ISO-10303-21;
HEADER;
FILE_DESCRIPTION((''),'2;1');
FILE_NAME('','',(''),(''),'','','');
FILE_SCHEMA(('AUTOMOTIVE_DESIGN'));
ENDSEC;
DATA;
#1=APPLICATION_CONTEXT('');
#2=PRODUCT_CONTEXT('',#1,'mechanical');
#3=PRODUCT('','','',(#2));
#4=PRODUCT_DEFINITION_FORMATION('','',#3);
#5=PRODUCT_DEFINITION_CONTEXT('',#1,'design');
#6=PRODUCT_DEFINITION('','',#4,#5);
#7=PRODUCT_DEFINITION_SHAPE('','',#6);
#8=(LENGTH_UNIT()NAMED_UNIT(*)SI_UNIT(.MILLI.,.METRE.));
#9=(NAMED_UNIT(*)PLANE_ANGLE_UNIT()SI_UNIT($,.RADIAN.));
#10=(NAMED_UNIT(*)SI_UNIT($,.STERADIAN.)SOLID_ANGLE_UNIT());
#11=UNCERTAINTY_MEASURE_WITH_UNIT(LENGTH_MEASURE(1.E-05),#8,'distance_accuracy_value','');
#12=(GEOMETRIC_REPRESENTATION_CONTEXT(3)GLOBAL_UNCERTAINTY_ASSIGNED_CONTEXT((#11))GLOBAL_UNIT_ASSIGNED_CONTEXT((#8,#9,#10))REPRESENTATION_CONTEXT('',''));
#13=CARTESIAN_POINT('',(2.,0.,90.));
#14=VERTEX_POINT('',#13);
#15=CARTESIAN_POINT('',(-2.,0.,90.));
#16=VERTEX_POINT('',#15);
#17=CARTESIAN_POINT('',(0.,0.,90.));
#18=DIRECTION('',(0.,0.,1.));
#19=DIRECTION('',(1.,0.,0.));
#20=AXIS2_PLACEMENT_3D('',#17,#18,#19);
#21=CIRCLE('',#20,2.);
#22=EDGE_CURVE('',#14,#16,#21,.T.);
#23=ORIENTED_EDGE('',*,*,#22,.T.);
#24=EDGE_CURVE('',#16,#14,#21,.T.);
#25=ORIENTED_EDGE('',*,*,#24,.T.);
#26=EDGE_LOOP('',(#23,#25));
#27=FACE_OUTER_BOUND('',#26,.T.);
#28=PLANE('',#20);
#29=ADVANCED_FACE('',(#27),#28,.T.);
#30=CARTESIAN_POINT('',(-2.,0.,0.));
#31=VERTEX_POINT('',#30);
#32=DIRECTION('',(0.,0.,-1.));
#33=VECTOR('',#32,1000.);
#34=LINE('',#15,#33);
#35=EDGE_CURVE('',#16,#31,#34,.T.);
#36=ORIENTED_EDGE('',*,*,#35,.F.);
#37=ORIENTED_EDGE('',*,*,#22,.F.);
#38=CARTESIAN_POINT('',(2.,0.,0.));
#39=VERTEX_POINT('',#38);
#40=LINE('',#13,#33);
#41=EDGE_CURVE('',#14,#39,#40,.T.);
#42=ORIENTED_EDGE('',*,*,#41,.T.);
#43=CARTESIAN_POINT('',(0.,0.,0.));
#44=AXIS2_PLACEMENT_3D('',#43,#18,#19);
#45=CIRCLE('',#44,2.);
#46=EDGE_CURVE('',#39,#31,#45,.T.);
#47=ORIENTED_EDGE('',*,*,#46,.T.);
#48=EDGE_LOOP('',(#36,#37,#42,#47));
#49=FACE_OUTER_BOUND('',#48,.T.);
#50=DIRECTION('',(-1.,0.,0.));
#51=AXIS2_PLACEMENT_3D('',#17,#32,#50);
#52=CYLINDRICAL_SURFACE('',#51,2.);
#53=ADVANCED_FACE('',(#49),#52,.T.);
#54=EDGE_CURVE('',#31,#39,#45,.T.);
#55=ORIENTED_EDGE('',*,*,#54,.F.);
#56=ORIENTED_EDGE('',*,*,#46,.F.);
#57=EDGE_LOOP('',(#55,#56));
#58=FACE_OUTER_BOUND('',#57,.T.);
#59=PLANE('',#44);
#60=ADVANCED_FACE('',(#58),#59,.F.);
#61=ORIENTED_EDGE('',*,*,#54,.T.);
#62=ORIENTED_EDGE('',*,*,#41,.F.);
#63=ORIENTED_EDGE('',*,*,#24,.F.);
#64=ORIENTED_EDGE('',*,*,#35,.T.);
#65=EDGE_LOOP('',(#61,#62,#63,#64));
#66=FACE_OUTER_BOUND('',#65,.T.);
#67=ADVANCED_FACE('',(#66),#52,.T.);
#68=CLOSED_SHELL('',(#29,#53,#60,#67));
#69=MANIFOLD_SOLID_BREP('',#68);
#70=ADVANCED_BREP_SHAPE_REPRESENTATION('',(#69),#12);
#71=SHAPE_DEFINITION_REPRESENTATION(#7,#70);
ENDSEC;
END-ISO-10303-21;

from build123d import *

# Parameters (mm, degrees)
SKETCH1_R           = 2
BOSS_EXTRUDE1_DEPTH = 90


with BuildPart() as part:
    # Sketch1 → Boss-Extrude1 (new body)
    with BuildSketch(Plane.XY):
        with Locations(Location((0, 0, 0), (0, 0, 180))):
            Circle(SKETCH1_R)
    extrude(amount=BOSS_EXTRUDE1_DEPTH)


solid = part.part
